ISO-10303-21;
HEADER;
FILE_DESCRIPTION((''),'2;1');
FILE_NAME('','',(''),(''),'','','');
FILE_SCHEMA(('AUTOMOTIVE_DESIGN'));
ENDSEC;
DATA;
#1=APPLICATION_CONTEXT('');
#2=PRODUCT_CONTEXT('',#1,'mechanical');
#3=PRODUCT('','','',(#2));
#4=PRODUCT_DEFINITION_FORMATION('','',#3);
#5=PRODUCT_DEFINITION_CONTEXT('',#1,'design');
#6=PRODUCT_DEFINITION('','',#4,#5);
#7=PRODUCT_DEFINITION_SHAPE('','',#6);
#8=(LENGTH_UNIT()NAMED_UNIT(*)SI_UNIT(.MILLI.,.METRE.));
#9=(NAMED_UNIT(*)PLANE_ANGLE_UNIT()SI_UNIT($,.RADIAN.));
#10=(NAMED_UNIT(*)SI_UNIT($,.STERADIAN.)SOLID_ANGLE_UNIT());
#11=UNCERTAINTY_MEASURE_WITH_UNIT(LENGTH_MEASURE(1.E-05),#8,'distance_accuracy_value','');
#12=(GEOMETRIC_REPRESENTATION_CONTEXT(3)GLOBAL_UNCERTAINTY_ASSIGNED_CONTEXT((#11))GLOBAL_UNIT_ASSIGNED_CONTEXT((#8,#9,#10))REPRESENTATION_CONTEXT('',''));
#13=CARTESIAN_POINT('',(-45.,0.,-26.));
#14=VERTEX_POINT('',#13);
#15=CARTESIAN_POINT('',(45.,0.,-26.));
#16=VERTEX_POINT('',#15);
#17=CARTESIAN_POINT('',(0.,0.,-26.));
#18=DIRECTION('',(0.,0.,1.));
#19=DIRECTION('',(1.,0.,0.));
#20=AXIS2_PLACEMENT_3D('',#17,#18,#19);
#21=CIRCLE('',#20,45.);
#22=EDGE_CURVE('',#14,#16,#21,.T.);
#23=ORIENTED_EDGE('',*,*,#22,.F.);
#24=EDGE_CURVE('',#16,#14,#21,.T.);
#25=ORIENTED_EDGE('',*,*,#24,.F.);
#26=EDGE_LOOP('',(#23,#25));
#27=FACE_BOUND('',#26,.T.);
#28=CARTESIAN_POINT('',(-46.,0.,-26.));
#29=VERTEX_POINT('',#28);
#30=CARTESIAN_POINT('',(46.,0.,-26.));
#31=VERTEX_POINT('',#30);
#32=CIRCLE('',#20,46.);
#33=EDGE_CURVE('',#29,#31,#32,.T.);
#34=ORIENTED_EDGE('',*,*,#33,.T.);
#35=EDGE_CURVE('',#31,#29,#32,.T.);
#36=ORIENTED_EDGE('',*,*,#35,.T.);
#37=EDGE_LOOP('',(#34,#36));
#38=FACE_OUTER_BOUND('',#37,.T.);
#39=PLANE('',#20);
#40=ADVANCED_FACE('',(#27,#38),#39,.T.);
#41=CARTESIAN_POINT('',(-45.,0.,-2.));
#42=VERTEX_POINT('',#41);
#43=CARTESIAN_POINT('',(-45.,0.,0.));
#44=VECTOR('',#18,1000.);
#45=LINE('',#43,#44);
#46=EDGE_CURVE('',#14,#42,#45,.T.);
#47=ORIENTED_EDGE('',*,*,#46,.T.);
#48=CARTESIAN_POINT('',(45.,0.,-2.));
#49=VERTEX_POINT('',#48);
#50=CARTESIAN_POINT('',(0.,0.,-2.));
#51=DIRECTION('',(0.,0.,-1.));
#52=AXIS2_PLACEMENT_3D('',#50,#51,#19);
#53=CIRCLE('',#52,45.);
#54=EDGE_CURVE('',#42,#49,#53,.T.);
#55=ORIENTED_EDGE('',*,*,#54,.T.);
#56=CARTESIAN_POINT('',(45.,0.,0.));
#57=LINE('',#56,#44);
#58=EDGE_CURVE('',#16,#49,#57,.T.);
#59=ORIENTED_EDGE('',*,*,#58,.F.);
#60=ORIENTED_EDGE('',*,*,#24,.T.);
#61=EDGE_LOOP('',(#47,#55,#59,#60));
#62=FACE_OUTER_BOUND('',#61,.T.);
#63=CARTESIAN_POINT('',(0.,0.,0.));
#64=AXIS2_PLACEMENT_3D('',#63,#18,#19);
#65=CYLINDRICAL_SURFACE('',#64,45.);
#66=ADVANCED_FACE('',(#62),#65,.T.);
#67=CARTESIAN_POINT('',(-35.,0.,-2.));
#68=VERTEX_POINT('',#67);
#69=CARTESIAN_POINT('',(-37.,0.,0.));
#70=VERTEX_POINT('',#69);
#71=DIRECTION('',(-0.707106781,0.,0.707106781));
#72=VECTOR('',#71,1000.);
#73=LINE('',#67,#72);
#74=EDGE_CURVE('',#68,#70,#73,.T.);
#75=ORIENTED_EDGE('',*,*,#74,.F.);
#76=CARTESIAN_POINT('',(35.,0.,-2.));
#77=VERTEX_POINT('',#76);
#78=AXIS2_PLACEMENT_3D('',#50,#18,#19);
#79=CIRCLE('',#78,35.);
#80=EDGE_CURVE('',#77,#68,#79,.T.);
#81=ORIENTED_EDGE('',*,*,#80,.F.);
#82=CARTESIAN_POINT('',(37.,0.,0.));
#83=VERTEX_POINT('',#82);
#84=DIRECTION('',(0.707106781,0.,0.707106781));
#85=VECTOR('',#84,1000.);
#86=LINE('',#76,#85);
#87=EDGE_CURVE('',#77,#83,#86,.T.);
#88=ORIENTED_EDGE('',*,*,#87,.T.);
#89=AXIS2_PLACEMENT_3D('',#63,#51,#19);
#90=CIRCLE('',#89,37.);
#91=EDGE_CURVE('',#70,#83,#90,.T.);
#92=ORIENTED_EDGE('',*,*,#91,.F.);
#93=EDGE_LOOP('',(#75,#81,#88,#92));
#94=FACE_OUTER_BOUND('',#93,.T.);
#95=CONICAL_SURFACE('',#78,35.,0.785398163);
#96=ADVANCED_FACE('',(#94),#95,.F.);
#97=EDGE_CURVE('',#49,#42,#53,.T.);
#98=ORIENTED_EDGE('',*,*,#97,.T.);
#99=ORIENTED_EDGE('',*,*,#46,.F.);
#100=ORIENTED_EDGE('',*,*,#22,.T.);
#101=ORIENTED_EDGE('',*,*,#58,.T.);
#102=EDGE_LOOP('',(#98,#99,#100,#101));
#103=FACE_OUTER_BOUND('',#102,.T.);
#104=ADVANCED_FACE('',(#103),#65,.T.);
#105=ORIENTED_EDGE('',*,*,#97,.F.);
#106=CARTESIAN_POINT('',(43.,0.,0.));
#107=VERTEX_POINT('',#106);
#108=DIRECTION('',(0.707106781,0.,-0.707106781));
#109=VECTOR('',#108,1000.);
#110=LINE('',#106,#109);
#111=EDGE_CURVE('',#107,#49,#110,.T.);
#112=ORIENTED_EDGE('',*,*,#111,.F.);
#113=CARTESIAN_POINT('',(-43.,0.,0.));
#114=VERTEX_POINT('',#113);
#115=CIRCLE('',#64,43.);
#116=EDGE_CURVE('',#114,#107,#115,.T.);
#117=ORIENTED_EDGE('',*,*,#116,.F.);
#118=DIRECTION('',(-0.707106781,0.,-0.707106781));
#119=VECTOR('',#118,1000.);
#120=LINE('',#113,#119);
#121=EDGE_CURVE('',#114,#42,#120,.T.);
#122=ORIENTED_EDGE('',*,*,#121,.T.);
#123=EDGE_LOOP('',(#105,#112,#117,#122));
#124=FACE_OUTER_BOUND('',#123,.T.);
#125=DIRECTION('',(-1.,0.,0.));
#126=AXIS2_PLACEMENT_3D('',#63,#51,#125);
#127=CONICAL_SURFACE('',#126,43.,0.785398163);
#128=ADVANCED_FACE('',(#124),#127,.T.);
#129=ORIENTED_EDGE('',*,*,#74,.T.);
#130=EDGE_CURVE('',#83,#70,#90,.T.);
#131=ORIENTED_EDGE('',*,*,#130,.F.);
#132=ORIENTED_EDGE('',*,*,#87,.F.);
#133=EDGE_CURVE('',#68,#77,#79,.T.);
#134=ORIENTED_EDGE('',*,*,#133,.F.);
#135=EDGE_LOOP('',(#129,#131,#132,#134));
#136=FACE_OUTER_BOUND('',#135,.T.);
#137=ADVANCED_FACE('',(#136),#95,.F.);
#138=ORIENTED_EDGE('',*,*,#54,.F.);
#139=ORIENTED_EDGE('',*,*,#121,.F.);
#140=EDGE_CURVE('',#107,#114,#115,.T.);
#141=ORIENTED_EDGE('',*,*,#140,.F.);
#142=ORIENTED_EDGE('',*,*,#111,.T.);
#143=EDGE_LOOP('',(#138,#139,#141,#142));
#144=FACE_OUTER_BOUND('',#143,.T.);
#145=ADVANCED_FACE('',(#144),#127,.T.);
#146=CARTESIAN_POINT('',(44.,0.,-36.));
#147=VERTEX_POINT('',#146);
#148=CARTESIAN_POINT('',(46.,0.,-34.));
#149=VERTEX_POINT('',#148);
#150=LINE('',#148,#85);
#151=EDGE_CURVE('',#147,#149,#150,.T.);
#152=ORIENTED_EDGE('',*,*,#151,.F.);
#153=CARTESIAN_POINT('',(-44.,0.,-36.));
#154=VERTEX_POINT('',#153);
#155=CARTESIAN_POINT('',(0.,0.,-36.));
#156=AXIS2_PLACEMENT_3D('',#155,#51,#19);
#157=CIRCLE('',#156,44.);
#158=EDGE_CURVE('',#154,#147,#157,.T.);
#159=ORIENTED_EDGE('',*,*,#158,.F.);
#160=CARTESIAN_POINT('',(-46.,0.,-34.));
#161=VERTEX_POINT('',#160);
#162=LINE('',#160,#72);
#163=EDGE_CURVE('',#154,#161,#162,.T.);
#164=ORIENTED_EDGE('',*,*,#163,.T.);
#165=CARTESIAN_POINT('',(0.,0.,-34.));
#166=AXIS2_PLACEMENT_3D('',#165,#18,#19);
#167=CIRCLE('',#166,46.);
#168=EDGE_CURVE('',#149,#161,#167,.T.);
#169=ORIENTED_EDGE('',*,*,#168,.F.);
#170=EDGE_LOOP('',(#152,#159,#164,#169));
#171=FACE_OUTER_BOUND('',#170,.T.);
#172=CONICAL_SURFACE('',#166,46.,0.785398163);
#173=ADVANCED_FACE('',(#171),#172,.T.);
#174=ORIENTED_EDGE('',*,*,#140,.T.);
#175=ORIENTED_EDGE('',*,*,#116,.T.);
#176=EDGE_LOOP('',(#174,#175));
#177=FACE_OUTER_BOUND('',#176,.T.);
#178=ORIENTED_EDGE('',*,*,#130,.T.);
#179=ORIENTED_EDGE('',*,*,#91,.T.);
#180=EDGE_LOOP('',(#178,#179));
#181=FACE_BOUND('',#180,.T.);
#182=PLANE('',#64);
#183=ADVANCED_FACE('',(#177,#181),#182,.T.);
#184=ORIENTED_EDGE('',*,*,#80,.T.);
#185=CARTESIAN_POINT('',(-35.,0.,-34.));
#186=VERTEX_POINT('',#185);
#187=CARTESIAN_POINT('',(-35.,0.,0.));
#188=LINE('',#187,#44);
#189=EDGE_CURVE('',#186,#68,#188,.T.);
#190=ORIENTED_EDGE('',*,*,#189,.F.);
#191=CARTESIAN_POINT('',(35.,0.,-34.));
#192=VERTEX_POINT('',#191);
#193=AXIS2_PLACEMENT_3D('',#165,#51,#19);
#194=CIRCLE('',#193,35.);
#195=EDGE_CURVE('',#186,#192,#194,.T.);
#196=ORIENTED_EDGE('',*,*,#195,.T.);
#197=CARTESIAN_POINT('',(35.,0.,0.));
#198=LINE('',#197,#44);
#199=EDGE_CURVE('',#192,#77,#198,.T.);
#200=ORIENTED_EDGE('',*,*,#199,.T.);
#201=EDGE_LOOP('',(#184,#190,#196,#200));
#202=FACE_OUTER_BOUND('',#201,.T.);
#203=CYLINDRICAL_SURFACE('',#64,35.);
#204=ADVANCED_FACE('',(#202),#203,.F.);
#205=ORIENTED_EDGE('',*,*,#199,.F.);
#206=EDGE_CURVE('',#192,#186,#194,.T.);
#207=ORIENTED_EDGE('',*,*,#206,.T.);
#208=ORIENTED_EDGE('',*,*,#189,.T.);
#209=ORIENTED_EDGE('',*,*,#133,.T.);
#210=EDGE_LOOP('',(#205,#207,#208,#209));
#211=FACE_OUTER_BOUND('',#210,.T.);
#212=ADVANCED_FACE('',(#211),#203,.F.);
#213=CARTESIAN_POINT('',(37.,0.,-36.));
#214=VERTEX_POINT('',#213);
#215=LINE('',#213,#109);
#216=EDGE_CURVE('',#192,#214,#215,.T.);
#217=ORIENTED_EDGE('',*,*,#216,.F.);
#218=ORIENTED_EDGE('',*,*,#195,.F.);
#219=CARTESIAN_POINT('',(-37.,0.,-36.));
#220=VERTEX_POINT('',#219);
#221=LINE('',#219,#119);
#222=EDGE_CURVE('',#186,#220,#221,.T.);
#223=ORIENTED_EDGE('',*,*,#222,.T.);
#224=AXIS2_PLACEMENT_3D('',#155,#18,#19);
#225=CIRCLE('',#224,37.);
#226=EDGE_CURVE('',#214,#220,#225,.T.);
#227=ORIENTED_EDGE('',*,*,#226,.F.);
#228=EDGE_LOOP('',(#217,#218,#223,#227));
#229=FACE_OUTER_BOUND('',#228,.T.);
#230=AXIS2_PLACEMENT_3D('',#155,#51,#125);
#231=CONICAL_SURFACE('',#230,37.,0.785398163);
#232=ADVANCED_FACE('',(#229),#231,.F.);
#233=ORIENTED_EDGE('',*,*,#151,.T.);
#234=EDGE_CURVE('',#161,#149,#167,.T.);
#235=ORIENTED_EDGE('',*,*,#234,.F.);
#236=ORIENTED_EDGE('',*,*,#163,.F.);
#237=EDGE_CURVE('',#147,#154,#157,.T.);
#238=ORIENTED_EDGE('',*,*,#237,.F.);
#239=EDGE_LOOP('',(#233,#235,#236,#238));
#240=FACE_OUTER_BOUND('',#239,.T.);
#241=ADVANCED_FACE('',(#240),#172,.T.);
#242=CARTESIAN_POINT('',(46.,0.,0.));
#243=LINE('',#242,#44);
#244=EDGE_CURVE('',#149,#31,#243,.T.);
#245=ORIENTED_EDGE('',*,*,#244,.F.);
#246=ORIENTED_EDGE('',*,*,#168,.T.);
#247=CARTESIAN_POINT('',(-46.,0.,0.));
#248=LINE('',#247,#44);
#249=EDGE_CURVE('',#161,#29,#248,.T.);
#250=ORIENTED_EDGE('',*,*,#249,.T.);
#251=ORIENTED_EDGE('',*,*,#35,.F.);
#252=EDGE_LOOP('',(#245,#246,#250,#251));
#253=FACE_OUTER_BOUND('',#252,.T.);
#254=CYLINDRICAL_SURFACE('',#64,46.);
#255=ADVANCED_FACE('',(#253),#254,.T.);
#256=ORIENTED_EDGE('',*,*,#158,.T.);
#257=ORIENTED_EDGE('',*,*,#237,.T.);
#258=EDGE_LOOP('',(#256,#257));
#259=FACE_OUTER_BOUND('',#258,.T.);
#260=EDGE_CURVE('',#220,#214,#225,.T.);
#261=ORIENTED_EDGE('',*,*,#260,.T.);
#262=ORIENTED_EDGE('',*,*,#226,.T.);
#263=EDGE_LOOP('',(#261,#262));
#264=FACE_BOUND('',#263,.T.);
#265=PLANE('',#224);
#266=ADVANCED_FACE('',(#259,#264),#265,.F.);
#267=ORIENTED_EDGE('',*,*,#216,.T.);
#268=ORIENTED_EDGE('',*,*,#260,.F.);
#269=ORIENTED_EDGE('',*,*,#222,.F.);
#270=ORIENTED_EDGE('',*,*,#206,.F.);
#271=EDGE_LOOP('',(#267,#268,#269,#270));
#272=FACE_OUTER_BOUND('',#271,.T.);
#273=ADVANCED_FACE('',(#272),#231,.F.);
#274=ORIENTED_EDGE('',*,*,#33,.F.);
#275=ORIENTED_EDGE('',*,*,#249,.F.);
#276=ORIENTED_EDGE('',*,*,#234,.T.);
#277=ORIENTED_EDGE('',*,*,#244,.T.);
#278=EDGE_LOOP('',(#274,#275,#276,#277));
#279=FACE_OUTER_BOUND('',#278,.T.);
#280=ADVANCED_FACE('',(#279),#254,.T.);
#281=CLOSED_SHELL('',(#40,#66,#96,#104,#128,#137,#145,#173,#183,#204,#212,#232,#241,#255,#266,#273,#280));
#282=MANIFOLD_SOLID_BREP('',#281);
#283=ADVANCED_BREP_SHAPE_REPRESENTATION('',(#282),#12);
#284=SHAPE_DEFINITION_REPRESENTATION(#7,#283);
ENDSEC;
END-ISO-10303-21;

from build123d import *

# Parameters (mm, degrees)
SKETCH1_W     = 26
SKETCH1_H     = 10
CHAMFER1_SIZE = 2


with BuildPart() as part:
    # Sketch1 → Revolve1 (revolve)
    with BuildSketch(Plane(origin=(0, 0, 0), x_dir=(0, 0, -1), z_dir=(1, 0, 0)), mode=Mode.PRIVATE) as revolve1_sk:
        with Locations((13, 40)):
            Rectangle(SKETCH1_W, SKETCH1_H)
        Polygon((26, 45), (26, 35), (36, 35), (36, 46), (26, 46), align=None)
    revolve(revolve1_sk.sketch.rotate(Axis((0, 0, 0), (0, 0, -1)), 90), axis=Axis((0, 0, 0), (0, 0, -1)))

    # Chamfer1
    chamfer1_edges = [part.edges().sort_by_distance(p)[0] for p in [
        (-45, 0, 0),
        (-46, 0, -36),
        (-35, 0, -36),
        (-35, 0, 0),
    ]]
    chamfer(chamfer1_edges, length=CHAMFER1_SIZE)


solid = part.part
